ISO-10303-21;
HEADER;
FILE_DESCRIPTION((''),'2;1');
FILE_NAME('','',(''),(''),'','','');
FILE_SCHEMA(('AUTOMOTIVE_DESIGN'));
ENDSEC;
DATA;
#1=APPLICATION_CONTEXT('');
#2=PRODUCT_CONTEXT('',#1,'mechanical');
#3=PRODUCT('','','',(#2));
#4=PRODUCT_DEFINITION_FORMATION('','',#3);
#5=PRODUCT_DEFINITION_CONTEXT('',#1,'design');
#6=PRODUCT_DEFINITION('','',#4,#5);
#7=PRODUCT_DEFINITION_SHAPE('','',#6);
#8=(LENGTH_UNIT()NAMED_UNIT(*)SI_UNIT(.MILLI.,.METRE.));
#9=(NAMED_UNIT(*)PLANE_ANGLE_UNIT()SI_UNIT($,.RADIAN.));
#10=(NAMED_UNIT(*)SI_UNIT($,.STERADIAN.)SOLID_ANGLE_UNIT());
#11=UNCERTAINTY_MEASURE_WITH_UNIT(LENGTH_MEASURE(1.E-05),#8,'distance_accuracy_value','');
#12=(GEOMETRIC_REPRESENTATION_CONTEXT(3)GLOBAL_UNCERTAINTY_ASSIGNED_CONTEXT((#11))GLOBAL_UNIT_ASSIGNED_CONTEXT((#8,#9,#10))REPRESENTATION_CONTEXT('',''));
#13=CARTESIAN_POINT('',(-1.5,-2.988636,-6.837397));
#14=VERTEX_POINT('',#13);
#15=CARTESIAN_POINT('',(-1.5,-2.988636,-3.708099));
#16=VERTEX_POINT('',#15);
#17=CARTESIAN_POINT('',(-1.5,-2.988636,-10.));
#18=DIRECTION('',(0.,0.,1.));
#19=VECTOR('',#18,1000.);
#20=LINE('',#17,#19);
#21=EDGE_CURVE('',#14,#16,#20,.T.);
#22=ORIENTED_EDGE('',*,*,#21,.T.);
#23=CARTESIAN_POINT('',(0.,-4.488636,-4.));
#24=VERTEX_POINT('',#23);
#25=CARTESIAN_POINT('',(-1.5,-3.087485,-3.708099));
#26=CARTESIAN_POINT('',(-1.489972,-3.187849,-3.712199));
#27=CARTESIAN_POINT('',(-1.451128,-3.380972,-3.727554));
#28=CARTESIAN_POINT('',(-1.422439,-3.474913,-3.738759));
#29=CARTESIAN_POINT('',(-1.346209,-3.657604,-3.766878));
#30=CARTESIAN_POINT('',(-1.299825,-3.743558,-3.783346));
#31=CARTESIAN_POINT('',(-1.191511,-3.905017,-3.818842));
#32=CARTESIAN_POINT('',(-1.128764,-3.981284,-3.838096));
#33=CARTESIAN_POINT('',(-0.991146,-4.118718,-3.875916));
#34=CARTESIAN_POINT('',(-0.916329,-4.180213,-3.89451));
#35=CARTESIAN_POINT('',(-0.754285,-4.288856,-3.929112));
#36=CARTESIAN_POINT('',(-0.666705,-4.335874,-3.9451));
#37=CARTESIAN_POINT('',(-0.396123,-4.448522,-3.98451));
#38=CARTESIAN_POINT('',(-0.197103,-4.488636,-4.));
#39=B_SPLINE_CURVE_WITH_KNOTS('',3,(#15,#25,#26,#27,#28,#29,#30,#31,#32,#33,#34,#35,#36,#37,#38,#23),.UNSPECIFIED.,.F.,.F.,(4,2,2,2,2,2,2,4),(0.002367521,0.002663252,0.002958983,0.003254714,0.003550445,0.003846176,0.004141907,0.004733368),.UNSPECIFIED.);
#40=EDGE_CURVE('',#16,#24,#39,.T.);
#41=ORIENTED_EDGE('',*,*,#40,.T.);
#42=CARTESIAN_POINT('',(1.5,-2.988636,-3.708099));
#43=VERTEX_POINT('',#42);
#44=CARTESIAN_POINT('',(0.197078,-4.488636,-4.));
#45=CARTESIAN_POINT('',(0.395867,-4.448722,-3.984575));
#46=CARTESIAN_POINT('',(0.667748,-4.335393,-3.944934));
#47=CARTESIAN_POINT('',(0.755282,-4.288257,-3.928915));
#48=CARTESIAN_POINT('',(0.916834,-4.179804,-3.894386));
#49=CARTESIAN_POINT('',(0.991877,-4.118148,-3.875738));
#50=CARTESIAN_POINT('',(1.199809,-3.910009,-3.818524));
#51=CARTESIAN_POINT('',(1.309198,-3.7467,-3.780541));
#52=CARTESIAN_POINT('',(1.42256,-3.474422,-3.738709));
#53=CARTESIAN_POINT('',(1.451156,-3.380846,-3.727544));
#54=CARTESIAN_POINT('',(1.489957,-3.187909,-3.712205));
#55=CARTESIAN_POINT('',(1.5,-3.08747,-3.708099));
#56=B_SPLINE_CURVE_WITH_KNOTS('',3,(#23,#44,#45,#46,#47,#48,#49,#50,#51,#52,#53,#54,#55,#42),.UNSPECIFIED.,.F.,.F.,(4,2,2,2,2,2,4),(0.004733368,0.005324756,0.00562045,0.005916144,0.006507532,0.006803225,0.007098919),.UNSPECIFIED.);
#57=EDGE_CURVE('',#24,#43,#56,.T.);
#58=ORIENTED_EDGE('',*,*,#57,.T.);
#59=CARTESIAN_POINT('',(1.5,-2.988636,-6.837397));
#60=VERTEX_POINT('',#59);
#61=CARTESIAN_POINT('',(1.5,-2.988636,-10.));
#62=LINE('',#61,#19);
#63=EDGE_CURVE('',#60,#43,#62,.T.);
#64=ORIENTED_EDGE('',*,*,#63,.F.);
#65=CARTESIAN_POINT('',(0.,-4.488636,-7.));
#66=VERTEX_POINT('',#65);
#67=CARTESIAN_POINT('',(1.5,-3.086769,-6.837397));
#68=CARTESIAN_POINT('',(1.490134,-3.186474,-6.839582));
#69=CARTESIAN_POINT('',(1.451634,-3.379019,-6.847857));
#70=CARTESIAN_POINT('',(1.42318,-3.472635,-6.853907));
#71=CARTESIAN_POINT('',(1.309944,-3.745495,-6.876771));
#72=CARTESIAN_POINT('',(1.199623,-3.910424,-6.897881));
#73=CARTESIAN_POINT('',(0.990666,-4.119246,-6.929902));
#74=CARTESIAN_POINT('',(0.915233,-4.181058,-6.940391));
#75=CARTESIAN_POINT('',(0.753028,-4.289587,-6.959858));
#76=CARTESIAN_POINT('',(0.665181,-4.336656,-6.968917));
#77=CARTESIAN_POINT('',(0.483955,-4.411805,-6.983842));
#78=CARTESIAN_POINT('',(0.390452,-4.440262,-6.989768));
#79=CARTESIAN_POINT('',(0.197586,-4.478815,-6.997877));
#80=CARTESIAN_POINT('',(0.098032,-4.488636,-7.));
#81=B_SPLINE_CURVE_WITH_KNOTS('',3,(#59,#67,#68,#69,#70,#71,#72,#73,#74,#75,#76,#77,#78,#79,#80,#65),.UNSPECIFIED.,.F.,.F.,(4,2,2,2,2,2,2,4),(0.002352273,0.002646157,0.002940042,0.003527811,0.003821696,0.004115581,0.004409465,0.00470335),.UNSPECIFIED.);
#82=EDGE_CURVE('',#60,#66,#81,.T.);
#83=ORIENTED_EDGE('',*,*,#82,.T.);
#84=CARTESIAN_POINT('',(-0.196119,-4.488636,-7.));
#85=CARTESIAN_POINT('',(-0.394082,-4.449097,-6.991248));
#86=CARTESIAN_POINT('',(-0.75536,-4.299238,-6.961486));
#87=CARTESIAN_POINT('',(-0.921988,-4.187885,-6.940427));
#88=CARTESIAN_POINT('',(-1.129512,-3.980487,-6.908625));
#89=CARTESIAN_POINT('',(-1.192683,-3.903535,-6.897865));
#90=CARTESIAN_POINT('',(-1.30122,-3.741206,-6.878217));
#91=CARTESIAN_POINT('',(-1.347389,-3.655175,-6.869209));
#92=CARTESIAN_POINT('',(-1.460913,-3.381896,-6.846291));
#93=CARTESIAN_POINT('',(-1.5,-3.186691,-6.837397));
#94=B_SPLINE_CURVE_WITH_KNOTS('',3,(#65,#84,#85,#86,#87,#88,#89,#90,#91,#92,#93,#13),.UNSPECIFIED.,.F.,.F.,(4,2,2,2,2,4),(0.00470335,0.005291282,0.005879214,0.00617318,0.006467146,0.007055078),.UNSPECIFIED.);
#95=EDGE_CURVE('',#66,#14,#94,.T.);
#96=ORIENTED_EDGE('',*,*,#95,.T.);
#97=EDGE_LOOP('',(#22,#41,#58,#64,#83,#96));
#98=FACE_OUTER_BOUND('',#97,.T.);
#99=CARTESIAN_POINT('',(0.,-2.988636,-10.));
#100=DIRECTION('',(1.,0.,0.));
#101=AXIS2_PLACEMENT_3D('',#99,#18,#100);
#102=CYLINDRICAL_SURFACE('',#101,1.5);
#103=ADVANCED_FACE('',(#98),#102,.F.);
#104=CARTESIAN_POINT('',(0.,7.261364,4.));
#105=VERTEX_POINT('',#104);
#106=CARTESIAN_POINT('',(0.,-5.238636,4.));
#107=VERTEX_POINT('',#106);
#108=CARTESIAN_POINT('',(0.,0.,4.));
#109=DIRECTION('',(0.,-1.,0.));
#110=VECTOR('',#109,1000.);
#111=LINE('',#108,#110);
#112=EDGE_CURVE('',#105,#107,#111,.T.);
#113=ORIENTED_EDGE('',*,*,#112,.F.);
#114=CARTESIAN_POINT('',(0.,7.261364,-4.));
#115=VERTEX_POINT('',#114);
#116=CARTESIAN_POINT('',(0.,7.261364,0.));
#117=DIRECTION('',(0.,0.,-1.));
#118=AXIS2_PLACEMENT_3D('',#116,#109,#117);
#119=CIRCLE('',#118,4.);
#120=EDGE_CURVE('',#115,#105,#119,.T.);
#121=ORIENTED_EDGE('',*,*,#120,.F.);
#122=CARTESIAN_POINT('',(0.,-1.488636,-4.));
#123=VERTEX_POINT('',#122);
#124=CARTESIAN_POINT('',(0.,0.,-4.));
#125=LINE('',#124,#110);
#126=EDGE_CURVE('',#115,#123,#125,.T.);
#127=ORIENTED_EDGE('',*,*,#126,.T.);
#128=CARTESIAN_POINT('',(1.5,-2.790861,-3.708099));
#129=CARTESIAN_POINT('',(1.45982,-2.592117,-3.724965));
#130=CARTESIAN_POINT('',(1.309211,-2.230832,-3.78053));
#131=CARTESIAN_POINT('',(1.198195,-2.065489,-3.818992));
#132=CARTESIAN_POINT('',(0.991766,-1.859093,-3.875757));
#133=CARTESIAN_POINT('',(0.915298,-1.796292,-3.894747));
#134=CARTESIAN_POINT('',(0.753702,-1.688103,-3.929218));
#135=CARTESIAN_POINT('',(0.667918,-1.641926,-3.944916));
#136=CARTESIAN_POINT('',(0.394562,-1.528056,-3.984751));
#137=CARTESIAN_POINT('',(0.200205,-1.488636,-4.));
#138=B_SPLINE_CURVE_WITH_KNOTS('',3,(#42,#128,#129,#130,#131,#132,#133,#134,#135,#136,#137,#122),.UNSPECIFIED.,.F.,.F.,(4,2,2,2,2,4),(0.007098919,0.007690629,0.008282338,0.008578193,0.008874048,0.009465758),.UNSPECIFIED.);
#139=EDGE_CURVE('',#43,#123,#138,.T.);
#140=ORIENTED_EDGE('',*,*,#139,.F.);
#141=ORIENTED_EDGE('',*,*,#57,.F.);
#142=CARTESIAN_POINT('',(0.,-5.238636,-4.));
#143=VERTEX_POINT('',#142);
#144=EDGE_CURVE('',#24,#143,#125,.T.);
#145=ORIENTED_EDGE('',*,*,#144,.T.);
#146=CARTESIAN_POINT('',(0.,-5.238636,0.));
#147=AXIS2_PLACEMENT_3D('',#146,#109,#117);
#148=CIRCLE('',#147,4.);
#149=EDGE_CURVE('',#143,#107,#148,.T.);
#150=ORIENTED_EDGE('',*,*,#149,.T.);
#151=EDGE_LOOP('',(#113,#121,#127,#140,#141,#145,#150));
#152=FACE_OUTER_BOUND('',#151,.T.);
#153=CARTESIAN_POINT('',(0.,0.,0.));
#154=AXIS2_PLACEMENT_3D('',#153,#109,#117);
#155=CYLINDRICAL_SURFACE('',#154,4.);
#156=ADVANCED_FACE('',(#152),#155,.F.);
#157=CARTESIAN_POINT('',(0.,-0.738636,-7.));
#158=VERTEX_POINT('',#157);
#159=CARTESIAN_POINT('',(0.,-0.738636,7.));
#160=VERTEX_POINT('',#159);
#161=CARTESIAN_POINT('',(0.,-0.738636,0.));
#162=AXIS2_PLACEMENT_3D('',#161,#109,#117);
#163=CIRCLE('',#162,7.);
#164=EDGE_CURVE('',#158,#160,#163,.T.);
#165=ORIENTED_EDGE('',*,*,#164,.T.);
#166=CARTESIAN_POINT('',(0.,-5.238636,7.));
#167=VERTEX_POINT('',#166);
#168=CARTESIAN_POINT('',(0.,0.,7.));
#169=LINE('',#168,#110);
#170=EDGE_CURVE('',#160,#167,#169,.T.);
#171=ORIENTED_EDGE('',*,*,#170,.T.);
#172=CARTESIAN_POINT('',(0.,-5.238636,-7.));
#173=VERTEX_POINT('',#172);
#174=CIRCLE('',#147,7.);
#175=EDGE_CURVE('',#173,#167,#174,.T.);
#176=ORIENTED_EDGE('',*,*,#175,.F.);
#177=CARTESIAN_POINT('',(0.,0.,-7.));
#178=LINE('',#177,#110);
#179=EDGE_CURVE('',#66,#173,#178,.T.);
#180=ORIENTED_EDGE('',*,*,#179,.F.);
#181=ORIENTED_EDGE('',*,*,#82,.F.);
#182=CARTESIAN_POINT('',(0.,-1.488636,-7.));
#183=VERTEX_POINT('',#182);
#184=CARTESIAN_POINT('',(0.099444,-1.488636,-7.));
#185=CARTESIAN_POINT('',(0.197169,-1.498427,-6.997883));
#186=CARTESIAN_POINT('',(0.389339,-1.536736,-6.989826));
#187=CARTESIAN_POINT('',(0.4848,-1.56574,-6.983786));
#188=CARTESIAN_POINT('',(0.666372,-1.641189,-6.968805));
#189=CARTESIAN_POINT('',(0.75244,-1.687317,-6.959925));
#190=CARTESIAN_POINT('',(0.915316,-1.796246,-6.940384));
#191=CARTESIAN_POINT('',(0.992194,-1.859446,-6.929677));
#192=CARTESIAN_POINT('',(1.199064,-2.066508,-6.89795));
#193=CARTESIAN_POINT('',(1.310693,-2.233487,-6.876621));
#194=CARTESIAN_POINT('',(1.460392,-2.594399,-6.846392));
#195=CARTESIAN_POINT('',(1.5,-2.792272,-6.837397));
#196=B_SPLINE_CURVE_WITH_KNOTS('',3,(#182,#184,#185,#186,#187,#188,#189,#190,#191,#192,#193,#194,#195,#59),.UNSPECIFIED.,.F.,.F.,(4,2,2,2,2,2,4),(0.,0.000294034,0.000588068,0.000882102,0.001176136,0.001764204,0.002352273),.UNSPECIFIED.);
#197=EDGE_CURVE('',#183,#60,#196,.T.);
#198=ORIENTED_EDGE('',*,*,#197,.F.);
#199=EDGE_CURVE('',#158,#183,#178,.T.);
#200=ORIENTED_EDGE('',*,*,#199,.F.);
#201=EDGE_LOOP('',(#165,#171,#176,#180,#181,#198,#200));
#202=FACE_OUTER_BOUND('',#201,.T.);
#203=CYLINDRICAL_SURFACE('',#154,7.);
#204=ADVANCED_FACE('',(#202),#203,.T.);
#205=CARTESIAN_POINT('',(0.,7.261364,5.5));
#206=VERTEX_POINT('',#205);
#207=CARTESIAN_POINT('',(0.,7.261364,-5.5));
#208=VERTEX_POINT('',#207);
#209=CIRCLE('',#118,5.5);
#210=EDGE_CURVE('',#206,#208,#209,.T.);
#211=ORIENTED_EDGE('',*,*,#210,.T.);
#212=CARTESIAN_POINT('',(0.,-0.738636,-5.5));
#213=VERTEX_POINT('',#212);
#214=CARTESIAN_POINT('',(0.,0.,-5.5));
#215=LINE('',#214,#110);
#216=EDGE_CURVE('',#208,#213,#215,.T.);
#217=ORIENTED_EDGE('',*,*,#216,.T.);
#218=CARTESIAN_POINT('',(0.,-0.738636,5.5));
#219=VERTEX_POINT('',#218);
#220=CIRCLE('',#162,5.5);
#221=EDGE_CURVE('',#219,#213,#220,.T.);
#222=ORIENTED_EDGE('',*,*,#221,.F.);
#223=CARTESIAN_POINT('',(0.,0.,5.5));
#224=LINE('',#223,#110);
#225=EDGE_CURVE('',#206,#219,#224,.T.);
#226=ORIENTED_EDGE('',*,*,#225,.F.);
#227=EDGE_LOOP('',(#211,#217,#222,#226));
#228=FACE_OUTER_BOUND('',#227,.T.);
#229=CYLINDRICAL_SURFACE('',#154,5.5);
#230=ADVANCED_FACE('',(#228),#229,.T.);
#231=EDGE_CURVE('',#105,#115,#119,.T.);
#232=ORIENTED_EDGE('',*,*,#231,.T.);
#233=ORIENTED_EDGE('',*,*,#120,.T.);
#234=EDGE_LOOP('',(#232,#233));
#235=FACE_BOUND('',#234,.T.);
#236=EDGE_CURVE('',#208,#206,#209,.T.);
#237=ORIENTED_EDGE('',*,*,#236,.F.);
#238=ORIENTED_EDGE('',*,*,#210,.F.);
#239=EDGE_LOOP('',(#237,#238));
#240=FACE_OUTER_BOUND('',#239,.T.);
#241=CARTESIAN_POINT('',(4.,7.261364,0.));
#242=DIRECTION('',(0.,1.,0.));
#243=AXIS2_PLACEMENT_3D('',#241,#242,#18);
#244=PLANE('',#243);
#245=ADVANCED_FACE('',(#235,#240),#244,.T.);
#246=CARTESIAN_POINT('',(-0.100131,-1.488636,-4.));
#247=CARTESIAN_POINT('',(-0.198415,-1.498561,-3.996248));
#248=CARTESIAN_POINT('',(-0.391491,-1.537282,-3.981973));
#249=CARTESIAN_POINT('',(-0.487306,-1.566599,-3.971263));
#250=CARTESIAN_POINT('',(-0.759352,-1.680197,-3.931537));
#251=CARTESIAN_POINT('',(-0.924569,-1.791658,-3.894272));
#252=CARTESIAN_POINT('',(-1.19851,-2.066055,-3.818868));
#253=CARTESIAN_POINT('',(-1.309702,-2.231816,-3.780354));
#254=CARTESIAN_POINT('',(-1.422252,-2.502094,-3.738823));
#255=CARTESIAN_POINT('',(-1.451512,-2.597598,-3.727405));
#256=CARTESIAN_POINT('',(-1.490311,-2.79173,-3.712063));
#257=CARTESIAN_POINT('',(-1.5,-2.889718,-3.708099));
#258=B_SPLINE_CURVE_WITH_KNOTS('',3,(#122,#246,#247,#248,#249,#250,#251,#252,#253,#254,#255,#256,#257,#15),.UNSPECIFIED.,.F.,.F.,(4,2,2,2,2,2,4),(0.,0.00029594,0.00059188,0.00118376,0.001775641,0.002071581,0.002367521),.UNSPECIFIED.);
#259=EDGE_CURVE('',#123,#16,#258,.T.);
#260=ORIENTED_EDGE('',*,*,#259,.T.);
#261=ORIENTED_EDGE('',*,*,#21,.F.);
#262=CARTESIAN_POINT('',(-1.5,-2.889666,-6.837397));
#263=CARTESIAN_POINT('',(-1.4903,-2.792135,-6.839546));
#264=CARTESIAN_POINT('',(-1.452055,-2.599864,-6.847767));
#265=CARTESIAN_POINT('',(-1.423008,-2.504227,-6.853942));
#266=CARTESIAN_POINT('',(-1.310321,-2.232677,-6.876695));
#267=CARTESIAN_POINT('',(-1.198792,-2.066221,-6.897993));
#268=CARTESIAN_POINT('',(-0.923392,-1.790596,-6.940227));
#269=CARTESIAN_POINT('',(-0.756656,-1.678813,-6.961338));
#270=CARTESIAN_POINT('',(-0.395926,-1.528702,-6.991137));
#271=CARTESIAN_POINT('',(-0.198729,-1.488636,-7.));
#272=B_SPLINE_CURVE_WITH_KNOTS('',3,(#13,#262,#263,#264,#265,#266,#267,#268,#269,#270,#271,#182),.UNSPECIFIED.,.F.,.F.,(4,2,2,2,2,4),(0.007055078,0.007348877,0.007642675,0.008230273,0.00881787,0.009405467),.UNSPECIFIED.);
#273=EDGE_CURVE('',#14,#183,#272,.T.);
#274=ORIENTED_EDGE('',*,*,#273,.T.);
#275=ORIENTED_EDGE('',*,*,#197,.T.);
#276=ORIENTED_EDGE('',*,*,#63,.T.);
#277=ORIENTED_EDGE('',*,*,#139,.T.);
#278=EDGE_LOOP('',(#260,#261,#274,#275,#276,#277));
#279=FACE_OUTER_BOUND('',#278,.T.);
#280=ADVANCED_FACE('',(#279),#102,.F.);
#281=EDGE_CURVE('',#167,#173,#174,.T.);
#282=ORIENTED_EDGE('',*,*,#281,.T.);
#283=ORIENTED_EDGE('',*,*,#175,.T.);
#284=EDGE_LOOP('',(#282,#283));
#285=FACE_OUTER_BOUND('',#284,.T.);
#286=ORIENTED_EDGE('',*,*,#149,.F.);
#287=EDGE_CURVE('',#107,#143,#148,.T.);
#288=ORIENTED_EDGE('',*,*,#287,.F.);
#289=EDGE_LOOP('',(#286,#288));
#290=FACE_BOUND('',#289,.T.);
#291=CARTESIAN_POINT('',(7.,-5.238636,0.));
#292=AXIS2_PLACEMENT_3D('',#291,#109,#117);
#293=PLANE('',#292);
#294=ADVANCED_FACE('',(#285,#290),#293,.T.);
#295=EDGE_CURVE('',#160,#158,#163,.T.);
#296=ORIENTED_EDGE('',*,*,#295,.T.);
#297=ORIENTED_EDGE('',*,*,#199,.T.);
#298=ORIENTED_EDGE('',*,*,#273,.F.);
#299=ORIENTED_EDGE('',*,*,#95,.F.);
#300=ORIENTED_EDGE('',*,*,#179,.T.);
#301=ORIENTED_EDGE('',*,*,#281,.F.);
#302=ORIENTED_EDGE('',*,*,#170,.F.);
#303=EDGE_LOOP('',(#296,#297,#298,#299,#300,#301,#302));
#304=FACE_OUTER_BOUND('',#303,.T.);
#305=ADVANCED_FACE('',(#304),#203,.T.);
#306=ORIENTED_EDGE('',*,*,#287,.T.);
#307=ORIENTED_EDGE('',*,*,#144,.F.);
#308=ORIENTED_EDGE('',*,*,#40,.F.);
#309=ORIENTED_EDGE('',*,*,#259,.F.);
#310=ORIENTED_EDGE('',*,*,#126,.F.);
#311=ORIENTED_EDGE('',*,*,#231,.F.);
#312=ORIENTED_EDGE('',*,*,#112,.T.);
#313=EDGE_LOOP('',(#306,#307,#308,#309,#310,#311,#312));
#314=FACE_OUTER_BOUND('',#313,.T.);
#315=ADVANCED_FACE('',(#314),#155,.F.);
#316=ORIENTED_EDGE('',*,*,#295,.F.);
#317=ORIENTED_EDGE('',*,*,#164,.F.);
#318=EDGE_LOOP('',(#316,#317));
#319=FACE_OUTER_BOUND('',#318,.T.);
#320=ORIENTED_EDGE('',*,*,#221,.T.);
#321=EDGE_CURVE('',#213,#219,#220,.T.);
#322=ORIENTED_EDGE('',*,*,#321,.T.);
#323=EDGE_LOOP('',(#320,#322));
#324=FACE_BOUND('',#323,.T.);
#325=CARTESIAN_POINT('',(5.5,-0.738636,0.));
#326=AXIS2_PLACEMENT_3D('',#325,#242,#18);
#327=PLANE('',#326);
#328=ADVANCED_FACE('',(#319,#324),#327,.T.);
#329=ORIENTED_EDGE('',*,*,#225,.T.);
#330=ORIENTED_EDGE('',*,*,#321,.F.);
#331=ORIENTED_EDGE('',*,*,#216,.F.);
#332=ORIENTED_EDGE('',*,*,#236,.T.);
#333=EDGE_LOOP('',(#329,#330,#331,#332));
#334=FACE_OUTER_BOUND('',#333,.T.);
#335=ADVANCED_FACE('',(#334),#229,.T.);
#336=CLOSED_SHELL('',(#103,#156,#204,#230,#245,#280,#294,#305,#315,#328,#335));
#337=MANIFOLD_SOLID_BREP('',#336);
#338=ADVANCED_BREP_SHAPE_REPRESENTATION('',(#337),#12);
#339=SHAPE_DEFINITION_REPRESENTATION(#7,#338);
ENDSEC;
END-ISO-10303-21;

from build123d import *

# Parameters (mm, degrees)
SKETCH_2_R          = 1.5
CUT_EXTRUDE_1_DEPTH = 10


with BuildPart() as part:
    # 草图1 → 旋转1 (revolve)
    with BuildSketch(Plane.XY, mode=Mode.PRIVATE) as revolve_1_sk:
        Polygon((4, 7.261363636), (5.5, 7.261363636), (5.5, -0.738636364), (7, -0.738636364), (7, -5.238636364), (4, -5.238636364), align=None)
    revolve(revolve_1_sk.sketch.rotate(Axis((0, 0, 0), (0, 1, 0)), 90), axis=Axis((0, 0, 0), (0, 1, 0)))

    # 草图2 → 切除-拉伸1 (cut)
    with BuildSketch(Plane.XY):
        with Locations(Location((0, -2.988636364, 0), (0, 0, 270.000000001))):
            Circle(SKETCH_2_R)
    extrude(amount=-CUT_EXTRUDE_1_DEPTH, mode=Mode.SUBTRACT)


solid = part.part
